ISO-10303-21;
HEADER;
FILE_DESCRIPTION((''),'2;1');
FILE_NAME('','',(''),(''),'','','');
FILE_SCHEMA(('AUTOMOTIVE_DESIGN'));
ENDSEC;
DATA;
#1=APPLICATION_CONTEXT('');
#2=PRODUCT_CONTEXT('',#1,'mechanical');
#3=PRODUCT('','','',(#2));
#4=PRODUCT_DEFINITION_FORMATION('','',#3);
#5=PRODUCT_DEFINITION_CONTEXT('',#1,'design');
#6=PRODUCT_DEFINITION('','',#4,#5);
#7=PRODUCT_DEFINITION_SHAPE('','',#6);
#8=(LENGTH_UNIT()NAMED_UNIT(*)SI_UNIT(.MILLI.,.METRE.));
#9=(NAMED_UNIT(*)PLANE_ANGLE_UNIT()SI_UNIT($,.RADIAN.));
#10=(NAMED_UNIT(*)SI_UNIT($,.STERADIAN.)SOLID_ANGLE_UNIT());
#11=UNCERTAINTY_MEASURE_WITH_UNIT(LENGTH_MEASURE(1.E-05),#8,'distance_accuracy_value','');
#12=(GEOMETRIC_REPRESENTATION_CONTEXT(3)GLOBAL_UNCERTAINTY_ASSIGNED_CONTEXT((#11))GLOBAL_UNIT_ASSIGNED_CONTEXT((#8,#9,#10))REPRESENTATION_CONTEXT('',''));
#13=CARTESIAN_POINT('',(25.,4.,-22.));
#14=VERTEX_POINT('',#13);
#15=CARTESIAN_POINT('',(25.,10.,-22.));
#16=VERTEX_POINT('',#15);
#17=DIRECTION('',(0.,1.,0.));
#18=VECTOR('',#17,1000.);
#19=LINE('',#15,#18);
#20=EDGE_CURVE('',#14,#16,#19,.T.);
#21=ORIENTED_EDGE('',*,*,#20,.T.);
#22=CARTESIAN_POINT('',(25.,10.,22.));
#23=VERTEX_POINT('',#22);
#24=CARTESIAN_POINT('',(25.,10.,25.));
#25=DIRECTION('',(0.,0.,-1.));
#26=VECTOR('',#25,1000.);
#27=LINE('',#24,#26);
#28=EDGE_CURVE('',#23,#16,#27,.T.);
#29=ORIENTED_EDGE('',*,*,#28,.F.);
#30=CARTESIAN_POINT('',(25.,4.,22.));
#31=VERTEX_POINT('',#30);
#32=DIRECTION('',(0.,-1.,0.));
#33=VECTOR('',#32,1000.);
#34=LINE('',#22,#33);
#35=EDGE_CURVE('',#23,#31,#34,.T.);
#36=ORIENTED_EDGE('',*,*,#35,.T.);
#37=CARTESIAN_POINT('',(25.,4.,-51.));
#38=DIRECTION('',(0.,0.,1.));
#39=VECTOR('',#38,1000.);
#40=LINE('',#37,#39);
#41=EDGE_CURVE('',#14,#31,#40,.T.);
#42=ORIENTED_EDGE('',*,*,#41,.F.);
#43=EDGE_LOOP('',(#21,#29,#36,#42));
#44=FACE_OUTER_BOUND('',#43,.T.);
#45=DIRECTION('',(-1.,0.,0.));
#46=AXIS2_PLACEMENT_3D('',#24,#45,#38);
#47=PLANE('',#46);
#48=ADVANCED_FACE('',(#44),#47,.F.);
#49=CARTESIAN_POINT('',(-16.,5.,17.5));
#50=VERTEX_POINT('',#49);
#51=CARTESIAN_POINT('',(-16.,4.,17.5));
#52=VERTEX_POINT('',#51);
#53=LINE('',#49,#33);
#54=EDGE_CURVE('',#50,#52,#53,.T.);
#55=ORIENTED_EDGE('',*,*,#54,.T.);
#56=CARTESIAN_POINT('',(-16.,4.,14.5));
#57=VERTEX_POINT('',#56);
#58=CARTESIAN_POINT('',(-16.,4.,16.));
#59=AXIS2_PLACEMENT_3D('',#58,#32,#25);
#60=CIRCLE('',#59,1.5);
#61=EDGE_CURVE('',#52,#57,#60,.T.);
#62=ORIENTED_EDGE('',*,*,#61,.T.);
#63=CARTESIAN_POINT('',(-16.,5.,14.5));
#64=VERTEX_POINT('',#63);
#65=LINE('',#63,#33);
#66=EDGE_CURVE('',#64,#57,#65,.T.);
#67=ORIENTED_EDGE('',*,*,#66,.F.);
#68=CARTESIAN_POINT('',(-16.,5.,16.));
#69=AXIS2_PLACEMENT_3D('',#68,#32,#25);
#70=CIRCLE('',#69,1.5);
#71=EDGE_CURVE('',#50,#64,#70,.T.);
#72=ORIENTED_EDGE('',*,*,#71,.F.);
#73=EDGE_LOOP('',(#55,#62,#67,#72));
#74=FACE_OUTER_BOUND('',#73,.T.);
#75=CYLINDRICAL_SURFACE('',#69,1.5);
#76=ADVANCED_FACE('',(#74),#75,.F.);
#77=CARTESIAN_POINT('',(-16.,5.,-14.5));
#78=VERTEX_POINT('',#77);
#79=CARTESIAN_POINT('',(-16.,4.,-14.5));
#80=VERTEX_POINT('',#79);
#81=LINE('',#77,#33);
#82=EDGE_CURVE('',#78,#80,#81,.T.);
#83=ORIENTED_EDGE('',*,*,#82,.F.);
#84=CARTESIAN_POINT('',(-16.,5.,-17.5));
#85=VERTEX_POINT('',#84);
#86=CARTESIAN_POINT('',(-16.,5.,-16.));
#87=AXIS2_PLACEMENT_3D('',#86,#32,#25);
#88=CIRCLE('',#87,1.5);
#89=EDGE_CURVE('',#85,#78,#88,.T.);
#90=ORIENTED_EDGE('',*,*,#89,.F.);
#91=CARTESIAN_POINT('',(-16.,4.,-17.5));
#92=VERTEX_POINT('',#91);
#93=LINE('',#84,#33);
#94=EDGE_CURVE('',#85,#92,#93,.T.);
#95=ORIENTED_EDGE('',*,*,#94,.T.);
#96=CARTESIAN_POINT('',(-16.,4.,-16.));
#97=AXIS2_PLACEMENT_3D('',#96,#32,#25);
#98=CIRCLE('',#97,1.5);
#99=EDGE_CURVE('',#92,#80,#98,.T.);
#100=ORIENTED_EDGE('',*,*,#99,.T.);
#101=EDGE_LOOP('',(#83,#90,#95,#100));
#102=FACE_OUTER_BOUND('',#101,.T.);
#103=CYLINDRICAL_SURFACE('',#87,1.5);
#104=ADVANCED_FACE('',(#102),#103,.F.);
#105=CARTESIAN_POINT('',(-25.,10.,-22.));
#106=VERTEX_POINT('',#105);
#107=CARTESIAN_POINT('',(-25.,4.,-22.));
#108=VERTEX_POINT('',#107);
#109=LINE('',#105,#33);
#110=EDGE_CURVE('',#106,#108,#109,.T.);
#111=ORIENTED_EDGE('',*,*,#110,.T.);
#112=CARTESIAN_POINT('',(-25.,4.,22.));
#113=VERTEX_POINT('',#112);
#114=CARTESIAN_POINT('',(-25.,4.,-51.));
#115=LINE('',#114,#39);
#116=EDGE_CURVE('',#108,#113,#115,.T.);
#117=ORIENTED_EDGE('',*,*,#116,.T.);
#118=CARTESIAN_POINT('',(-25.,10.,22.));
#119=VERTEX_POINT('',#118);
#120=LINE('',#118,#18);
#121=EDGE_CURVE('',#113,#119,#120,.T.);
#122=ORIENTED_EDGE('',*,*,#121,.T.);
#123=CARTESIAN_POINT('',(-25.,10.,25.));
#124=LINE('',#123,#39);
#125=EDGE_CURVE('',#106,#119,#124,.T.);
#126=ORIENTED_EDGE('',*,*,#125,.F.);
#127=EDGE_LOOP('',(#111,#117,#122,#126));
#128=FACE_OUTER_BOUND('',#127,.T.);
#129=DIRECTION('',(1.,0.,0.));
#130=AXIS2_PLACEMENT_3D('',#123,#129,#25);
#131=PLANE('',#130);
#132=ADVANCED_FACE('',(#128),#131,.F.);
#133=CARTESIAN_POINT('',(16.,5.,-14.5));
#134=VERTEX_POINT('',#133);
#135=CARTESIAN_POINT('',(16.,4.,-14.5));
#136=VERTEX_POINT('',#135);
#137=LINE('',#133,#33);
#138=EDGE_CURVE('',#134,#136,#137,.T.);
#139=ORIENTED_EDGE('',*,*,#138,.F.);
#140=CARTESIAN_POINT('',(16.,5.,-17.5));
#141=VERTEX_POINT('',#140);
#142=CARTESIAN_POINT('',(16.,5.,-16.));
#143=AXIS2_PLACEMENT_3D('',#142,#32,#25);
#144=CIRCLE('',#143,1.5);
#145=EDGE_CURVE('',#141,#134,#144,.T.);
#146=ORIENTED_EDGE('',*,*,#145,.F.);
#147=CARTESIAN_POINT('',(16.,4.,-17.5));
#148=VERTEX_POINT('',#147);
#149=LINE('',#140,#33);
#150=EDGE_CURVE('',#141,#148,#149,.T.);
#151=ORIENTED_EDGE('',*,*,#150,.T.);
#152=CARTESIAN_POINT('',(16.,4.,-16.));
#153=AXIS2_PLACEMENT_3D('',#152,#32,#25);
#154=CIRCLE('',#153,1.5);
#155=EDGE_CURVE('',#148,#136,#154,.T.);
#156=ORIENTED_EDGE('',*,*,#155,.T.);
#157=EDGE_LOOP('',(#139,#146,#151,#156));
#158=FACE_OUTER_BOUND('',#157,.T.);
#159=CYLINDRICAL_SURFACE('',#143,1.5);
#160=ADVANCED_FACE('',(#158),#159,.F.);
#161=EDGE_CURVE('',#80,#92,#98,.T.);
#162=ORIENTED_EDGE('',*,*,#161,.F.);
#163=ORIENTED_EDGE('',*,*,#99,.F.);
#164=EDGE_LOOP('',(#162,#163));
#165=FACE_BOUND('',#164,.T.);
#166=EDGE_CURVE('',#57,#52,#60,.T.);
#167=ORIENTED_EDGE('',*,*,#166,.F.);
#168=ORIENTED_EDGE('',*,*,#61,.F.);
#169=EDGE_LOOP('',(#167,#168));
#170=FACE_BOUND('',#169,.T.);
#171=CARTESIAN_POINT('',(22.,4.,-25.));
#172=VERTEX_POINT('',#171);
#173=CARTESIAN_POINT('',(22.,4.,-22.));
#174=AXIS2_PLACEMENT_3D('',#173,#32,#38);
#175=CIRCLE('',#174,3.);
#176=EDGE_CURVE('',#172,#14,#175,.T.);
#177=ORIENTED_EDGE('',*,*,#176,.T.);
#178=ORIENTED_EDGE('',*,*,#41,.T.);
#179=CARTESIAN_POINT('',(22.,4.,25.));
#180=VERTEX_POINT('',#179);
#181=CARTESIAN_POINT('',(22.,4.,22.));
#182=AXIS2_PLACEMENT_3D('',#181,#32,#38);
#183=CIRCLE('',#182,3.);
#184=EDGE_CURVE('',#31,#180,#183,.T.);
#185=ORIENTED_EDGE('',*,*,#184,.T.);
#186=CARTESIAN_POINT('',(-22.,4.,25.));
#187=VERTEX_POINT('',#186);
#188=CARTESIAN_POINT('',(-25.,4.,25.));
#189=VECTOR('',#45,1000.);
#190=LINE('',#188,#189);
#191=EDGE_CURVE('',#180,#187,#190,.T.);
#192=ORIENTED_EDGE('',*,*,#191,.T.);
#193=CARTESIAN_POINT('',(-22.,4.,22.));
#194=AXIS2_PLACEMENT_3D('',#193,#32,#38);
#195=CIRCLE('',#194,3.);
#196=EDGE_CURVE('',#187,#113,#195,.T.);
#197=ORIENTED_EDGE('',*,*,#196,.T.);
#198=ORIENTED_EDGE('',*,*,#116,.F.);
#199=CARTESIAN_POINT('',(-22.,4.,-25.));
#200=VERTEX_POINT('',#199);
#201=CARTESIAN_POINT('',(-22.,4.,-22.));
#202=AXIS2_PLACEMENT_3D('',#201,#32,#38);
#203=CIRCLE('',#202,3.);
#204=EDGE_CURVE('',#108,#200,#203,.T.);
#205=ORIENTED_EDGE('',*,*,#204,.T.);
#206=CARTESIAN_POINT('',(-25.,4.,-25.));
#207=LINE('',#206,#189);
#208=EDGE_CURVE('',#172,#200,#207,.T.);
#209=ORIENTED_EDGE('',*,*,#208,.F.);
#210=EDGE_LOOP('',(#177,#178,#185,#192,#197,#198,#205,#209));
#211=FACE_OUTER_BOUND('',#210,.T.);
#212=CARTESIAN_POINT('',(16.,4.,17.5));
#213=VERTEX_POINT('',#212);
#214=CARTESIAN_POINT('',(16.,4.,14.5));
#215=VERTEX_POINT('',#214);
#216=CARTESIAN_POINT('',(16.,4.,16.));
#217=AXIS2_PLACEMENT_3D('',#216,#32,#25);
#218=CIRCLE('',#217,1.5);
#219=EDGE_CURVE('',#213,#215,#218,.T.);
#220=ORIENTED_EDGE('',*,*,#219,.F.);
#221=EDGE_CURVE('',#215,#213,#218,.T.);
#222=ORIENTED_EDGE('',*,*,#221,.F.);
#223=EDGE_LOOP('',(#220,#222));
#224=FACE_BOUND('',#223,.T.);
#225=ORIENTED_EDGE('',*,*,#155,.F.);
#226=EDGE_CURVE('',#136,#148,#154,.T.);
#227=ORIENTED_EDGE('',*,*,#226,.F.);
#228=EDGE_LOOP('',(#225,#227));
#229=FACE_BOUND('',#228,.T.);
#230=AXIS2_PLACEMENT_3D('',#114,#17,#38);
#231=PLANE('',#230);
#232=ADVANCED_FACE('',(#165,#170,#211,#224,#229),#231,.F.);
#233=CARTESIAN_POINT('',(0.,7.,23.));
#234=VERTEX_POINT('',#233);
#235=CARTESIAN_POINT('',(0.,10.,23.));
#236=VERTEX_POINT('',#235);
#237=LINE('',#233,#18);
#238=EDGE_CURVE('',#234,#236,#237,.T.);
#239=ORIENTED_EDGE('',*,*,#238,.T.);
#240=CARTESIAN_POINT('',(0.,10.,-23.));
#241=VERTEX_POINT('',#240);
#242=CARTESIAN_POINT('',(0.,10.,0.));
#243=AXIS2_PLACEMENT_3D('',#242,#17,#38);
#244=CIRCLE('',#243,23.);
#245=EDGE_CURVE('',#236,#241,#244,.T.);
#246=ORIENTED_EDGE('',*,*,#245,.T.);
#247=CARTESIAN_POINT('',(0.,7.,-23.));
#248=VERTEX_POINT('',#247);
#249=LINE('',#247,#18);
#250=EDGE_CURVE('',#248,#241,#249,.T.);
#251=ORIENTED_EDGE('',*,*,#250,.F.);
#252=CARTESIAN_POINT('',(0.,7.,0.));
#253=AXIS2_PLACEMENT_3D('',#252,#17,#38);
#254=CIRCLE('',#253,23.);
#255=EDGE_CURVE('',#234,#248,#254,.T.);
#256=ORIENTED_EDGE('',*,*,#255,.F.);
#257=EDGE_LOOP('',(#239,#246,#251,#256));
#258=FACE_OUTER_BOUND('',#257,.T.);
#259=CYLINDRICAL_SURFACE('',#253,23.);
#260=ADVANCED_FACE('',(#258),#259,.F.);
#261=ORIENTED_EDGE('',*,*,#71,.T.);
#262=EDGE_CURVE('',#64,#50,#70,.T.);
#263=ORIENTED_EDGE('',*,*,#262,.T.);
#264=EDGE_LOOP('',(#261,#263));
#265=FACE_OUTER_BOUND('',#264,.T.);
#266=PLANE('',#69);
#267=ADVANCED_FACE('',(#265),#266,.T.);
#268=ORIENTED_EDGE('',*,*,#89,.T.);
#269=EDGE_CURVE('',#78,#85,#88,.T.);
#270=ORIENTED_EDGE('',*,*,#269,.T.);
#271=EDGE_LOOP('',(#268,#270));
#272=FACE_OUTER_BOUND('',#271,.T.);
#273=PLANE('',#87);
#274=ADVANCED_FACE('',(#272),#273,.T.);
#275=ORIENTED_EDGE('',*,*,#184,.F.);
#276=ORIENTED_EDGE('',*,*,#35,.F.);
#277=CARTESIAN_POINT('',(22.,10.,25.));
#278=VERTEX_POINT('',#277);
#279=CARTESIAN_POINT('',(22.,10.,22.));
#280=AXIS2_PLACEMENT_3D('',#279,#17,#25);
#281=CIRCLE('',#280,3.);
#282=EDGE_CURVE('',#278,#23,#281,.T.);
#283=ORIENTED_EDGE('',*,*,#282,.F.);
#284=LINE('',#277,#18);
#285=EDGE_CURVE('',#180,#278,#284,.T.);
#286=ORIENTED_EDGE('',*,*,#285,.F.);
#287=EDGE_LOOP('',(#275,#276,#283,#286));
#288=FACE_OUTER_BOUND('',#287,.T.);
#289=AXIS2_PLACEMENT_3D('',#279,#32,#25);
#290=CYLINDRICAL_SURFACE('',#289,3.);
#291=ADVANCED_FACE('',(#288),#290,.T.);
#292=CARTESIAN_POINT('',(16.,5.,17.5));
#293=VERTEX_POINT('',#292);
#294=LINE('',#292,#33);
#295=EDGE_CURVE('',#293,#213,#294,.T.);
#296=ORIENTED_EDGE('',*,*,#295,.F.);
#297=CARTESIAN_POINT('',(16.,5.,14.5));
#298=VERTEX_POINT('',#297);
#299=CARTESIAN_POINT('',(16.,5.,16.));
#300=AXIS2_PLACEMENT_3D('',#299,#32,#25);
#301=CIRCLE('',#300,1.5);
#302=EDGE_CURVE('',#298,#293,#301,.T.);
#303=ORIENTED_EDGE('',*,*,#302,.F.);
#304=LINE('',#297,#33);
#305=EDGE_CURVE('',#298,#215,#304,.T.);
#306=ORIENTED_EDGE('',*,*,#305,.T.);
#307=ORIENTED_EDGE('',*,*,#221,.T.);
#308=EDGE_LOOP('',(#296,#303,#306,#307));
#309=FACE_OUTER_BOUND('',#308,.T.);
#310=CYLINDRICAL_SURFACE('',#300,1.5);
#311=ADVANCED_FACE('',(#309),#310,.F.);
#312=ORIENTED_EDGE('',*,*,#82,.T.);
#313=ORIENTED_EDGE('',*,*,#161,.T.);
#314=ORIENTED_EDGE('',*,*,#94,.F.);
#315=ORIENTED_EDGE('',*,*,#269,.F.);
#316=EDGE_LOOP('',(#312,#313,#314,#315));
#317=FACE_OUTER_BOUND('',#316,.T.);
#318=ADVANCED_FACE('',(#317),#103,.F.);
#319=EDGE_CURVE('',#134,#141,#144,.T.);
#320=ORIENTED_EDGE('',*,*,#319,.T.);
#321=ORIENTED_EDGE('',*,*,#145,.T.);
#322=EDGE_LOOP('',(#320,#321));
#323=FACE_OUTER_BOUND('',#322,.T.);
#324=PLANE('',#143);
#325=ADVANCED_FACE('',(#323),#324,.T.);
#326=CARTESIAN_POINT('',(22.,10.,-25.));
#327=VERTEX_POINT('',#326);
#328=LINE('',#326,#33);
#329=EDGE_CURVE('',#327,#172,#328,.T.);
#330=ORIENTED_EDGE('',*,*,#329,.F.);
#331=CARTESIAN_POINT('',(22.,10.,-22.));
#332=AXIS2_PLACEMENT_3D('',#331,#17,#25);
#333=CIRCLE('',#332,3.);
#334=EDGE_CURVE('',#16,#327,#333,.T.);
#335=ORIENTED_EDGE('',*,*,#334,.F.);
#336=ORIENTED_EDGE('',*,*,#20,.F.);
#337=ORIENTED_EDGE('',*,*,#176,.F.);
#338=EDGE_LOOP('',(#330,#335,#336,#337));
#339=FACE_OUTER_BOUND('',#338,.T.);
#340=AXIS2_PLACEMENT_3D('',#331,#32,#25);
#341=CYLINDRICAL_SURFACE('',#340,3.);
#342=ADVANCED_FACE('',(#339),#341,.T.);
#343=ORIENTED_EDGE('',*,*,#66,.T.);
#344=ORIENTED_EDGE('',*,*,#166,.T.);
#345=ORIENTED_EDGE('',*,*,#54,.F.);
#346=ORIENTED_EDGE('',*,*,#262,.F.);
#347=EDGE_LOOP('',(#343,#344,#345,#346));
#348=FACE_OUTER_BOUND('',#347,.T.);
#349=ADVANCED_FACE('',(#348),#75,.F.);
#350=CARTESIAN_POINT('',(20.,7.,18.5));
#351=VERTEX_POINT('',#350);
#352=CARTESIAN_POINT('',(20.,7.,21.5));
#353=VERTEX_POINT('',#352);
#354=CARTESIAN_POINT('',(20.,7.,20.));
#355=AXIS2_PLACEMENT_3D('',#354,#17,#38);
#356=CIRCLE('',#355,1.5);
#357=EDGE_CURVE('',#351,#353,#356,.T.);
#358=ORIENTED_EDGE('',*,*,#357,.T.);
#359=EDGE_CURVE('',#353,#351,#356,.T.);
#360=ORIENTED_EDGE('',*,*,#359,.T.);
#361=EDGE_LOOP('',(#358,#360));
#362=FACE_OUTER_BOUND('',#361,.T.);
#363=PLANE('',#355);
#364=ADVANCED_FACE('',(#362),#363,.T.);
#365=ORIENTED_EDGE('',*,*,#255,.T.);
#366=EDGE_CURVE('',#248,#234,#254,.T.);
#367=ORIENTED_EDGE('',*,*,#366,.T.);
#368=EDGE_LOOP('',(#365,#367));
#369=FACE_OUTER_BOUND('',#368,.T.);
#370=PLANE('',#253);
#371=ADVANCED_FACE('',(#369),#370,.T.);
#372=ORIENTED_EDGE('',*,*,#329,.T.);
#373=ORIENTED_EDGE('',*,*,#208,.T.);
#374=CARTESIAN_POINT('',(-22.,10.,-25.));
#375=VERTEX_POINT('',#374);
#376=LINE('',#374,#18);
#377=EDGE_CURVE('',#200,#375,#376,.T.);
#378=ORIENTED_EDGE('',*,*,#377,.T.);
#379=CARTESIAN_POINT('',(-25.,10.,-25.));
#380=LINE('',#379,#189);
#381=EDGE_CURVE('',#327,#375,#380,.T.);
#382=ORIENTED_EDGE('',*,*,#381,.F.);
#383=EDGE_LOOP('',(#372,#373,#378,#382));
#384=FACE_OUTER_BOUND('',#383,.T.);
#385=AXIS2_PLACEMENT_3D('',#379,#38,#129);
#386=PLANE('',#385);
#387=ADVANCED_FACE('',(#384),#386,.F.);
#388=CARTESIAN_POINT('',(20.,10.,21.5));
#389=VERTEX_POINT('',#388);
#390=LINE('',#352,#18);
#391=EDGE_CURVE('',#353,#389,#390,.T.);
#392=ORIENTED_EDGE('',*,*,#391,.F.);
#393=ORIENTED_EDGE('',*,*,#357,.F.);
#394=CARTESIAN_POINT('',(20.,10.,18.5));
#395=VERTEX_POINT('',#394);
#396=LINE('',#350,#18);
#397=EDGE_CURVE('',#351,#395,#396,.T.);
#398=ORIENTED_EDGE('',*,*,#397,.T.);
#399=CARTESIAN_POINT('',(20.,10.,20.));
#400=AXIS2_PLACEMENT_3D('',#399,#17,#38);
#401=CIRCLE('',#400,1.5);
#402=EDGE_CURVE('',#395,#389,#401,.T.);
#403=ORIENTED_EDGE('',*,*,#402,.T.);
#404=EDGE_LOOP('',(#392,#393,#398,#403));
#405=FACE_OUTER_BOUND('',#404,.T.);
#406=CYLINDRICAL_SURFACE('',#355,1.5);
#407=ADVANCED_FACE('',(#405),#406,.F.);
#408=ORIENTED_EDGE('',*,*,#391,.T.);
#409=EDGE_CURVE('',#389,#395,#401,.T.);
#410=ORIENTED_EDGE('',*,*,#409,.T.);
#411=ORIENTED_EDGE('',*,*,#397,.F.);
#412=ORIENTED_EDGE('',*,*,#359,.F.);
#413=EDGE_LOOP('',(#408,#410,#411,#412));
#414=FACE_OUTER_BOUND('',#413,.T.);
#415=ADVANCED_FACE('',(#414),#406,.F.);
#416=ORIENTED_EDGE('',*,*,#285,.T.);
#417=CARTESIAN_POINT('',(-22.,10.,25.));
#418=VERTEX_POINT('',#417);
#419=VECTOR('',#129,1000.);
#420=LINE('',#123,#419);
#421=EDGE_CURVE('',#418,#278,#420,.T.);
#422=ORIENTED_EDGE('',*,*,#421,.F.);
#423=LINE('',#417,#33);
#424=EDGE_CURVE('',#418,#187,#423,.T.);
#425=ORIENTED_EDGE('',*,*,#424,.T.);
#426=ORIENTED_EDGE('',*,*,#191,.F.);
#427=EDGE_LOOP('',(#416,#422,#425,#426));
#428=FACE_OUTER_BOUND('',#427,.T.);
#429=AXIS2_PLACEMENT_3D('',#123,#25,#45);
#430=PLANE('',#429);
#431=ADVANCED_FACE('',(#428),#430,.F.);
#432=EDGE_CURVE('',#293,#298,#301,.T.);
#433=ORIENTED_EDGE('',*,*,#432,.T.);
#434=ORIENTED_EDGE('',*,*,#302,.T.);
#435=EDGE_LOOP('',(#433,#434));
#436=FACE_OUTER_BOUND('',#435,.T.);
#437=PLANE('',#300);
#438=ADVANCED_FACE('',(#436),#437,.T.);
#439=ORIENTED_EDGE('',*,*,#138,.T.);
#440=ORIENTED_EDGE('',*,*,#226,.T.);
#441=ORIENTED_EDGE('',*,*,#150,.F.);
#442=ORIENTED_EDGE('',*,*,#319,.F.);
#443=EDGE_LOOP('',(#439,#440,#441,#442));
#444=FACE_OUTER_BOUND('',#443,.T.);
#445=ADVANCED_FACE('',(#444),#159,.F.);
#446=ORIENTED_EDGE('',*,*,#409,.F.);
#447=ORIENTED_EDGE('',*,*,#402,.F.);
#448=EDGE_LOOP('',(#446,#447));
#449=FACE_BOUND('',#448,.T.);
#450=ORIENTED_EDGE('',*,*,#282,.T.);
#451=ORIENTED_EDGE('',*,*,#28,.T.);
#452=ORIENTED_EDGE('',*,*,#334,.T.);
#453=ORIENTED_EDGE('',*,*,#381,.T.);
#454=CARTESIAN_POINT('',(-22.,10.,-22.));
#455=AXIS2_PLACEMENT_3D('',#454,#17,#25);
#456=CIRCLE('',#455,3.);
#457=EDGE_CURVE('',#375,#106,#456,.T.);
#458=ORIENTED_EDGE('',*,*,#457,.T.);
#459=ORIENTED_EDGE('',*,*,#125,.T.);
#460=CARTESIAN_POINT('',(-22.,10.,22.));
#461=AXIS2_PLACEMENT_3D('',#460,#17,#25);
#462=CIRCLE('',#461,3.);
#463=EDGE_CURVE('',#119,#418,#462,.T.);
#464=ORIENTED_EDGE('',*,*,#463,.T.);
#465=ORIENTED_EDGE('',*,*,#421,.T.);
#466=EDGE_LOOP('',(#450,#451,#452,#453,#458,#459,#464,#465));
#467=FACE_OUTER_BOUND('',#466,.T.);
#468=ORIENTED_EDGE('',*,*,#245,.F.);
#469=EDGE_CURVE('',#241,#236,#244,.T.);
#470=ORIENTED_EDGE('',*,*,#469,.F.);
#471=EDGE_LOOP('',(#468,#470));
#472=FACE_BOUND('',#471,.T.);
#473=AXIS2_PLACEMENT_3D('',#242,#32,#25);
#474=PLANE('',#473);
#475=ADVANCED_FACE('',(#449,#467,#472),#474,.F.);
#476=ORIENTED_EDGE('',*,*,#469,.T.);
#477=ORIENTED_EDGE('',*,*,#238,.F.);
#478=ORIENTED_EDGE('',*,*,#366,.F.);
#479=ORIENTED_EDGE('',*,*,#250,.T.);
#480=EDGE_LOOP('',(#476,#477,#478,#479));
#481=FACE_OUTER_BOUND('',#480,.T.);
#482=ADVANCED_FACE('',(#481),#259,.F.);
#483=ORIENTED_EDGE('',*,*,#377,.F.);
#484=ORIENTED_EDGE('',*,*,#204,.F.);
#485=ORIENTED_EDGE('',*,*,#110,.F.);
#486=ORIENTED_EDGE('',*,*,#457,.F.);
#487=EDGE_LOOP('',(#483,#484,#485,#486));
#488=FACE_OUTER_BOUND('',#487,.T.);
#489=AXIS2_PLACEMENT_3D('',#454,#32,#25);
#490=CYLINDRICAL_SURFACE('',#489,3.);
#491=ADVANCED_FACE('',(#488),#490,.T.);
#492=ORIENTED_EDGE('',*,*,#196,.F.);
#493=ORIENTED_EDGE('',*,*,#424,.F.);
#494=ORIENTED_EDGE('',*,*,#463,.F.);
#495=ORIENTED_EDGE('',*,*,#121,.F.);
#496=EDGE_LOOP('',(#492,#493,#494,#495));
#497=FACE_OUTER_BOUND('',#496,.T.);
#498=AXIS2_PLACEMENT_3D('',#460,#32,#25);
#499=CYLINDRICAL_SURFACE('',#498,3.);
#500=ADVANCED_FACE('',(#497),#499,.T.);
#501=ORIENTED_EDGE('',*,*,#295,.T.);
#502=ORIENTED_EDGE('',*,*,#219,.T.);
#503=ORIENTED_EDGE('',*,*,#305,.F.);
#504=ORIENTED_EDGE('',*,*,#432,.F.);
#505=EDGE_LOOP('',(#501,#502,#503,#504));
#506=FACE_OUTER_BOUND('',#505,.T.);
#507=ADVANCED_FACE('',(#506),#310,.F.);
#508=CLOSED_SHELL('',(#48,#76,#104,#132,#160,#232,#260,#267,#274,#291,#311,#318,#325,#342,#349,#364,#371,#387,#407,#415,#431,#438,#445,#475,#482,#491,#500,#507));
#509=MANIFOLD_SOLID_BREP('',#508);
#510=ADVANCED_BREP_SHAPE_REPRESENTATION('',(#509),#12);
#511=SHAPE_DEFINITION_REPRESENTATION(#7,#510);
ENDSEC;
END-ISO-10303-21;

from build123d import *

# Parameters (mm, degrees)
SKETCH1_W           = 50
SKETCH1_H           = 50
BOSS_EXTRUDE1_DEPTH = 10
SKETCH2_R           = 23
CUT_EXTRUDE1_DEPTH  = 3
SKETCH3_R           = 1.5
CUT_EXTRUDE2_DEPTH  = 3
SKETCH4_W           = 50
SKETCH4_H           = 4
CUT_EXTRUDE3_DEPTH  = 76
FILLET1_R           = 3
SKETCH5_R           = 1.5
CUT_EXTRUDE4_DEPTH  = 1


with BuildPart() as part:
    # Sketch1 → Boss-Extrude1 (new body)
    with BuildSketch(Plane(origin=(0, 0, 0), x_dir=(1, 0, 0), z_dir=(0, 1, 0))):
        Rectangle(SKETCH1_W, SKETCH1_H)
    extrude(amount=BOSS_EXTRUDE1_DEPTH)

    # Sketch2 → Cut-Extrude1 (cut)
    with BuildSketch(Plane(origin=(0, 10, 0), x_dir=(1, 0, 0), z_dir=(0, 1, 0))):
        with Locations(Location((0, 0, 0), (0, 0, 270))):
            Circle(SKETCH2_R)
    extrude(amount=-CUT_EXTRUDE1_DEPTH, mode=Mode.SUBTRACT)

    # Sketch3 → Cut-Extrude2 (cut)
    with BuildSketch(Plane(origin=(0, 10, 0), x_dir=(1, 0, 0), z_dir=(0, 1, 0))):
        with Locations(Location((20, -20, 0), (0, 0, 270))):
            Circle(SKETCH3_R)
    extrude(amount=-CUT_EXTRUDE2_DEPTH, mode=Mode.SUBTRACT)

    # Sketch4 → Cut-Extrude3 (cut)
    with BuildSketch(Plane.XY.offset(25)):
        with Locations((0, 2)):
            Rectangle(SKETCH4_W, SKETCH4_H)
    extrude(amount=-CUT_EXTRUDE3_DEPTH, mode=Mode.SUBTRACT)

    # Fillet1
    fillet1_edges = [part.edges().sort_by_distance(p)[0] for p in [
        (25, 7, 25),
        (-25, 7, 25),
        (-25, 7, -25),
        (25, 7, -25),
    ]]
    fillet(fillet1_edges, radius=FILLET1_R)

    # Sketch5 → Cut-Extrude4 (cut)
    with BuildSketch(Plane.XZ.offset(-4)):
        with Locations(Location((-16, 16, 0), (0, 0, 270))):
            Circle(SKETCH5_R)
        with Locations(Location((16, 16, 0), (0, 0, 270))):
            Circle(SKETCH5_R)
        with Locations(Location((-16, -16, 0), (0, 0, 270))):
            Circle(SKETCH5_R)
        with Locations(Location((16, -16, 0), (0, 0, 270))):
            Circle(SKETCH5_R)
    extrude(amount=-CUT_EXTRUDE4_DEPTH, mode=Mode.SUBTRACT)


solid = part.part
